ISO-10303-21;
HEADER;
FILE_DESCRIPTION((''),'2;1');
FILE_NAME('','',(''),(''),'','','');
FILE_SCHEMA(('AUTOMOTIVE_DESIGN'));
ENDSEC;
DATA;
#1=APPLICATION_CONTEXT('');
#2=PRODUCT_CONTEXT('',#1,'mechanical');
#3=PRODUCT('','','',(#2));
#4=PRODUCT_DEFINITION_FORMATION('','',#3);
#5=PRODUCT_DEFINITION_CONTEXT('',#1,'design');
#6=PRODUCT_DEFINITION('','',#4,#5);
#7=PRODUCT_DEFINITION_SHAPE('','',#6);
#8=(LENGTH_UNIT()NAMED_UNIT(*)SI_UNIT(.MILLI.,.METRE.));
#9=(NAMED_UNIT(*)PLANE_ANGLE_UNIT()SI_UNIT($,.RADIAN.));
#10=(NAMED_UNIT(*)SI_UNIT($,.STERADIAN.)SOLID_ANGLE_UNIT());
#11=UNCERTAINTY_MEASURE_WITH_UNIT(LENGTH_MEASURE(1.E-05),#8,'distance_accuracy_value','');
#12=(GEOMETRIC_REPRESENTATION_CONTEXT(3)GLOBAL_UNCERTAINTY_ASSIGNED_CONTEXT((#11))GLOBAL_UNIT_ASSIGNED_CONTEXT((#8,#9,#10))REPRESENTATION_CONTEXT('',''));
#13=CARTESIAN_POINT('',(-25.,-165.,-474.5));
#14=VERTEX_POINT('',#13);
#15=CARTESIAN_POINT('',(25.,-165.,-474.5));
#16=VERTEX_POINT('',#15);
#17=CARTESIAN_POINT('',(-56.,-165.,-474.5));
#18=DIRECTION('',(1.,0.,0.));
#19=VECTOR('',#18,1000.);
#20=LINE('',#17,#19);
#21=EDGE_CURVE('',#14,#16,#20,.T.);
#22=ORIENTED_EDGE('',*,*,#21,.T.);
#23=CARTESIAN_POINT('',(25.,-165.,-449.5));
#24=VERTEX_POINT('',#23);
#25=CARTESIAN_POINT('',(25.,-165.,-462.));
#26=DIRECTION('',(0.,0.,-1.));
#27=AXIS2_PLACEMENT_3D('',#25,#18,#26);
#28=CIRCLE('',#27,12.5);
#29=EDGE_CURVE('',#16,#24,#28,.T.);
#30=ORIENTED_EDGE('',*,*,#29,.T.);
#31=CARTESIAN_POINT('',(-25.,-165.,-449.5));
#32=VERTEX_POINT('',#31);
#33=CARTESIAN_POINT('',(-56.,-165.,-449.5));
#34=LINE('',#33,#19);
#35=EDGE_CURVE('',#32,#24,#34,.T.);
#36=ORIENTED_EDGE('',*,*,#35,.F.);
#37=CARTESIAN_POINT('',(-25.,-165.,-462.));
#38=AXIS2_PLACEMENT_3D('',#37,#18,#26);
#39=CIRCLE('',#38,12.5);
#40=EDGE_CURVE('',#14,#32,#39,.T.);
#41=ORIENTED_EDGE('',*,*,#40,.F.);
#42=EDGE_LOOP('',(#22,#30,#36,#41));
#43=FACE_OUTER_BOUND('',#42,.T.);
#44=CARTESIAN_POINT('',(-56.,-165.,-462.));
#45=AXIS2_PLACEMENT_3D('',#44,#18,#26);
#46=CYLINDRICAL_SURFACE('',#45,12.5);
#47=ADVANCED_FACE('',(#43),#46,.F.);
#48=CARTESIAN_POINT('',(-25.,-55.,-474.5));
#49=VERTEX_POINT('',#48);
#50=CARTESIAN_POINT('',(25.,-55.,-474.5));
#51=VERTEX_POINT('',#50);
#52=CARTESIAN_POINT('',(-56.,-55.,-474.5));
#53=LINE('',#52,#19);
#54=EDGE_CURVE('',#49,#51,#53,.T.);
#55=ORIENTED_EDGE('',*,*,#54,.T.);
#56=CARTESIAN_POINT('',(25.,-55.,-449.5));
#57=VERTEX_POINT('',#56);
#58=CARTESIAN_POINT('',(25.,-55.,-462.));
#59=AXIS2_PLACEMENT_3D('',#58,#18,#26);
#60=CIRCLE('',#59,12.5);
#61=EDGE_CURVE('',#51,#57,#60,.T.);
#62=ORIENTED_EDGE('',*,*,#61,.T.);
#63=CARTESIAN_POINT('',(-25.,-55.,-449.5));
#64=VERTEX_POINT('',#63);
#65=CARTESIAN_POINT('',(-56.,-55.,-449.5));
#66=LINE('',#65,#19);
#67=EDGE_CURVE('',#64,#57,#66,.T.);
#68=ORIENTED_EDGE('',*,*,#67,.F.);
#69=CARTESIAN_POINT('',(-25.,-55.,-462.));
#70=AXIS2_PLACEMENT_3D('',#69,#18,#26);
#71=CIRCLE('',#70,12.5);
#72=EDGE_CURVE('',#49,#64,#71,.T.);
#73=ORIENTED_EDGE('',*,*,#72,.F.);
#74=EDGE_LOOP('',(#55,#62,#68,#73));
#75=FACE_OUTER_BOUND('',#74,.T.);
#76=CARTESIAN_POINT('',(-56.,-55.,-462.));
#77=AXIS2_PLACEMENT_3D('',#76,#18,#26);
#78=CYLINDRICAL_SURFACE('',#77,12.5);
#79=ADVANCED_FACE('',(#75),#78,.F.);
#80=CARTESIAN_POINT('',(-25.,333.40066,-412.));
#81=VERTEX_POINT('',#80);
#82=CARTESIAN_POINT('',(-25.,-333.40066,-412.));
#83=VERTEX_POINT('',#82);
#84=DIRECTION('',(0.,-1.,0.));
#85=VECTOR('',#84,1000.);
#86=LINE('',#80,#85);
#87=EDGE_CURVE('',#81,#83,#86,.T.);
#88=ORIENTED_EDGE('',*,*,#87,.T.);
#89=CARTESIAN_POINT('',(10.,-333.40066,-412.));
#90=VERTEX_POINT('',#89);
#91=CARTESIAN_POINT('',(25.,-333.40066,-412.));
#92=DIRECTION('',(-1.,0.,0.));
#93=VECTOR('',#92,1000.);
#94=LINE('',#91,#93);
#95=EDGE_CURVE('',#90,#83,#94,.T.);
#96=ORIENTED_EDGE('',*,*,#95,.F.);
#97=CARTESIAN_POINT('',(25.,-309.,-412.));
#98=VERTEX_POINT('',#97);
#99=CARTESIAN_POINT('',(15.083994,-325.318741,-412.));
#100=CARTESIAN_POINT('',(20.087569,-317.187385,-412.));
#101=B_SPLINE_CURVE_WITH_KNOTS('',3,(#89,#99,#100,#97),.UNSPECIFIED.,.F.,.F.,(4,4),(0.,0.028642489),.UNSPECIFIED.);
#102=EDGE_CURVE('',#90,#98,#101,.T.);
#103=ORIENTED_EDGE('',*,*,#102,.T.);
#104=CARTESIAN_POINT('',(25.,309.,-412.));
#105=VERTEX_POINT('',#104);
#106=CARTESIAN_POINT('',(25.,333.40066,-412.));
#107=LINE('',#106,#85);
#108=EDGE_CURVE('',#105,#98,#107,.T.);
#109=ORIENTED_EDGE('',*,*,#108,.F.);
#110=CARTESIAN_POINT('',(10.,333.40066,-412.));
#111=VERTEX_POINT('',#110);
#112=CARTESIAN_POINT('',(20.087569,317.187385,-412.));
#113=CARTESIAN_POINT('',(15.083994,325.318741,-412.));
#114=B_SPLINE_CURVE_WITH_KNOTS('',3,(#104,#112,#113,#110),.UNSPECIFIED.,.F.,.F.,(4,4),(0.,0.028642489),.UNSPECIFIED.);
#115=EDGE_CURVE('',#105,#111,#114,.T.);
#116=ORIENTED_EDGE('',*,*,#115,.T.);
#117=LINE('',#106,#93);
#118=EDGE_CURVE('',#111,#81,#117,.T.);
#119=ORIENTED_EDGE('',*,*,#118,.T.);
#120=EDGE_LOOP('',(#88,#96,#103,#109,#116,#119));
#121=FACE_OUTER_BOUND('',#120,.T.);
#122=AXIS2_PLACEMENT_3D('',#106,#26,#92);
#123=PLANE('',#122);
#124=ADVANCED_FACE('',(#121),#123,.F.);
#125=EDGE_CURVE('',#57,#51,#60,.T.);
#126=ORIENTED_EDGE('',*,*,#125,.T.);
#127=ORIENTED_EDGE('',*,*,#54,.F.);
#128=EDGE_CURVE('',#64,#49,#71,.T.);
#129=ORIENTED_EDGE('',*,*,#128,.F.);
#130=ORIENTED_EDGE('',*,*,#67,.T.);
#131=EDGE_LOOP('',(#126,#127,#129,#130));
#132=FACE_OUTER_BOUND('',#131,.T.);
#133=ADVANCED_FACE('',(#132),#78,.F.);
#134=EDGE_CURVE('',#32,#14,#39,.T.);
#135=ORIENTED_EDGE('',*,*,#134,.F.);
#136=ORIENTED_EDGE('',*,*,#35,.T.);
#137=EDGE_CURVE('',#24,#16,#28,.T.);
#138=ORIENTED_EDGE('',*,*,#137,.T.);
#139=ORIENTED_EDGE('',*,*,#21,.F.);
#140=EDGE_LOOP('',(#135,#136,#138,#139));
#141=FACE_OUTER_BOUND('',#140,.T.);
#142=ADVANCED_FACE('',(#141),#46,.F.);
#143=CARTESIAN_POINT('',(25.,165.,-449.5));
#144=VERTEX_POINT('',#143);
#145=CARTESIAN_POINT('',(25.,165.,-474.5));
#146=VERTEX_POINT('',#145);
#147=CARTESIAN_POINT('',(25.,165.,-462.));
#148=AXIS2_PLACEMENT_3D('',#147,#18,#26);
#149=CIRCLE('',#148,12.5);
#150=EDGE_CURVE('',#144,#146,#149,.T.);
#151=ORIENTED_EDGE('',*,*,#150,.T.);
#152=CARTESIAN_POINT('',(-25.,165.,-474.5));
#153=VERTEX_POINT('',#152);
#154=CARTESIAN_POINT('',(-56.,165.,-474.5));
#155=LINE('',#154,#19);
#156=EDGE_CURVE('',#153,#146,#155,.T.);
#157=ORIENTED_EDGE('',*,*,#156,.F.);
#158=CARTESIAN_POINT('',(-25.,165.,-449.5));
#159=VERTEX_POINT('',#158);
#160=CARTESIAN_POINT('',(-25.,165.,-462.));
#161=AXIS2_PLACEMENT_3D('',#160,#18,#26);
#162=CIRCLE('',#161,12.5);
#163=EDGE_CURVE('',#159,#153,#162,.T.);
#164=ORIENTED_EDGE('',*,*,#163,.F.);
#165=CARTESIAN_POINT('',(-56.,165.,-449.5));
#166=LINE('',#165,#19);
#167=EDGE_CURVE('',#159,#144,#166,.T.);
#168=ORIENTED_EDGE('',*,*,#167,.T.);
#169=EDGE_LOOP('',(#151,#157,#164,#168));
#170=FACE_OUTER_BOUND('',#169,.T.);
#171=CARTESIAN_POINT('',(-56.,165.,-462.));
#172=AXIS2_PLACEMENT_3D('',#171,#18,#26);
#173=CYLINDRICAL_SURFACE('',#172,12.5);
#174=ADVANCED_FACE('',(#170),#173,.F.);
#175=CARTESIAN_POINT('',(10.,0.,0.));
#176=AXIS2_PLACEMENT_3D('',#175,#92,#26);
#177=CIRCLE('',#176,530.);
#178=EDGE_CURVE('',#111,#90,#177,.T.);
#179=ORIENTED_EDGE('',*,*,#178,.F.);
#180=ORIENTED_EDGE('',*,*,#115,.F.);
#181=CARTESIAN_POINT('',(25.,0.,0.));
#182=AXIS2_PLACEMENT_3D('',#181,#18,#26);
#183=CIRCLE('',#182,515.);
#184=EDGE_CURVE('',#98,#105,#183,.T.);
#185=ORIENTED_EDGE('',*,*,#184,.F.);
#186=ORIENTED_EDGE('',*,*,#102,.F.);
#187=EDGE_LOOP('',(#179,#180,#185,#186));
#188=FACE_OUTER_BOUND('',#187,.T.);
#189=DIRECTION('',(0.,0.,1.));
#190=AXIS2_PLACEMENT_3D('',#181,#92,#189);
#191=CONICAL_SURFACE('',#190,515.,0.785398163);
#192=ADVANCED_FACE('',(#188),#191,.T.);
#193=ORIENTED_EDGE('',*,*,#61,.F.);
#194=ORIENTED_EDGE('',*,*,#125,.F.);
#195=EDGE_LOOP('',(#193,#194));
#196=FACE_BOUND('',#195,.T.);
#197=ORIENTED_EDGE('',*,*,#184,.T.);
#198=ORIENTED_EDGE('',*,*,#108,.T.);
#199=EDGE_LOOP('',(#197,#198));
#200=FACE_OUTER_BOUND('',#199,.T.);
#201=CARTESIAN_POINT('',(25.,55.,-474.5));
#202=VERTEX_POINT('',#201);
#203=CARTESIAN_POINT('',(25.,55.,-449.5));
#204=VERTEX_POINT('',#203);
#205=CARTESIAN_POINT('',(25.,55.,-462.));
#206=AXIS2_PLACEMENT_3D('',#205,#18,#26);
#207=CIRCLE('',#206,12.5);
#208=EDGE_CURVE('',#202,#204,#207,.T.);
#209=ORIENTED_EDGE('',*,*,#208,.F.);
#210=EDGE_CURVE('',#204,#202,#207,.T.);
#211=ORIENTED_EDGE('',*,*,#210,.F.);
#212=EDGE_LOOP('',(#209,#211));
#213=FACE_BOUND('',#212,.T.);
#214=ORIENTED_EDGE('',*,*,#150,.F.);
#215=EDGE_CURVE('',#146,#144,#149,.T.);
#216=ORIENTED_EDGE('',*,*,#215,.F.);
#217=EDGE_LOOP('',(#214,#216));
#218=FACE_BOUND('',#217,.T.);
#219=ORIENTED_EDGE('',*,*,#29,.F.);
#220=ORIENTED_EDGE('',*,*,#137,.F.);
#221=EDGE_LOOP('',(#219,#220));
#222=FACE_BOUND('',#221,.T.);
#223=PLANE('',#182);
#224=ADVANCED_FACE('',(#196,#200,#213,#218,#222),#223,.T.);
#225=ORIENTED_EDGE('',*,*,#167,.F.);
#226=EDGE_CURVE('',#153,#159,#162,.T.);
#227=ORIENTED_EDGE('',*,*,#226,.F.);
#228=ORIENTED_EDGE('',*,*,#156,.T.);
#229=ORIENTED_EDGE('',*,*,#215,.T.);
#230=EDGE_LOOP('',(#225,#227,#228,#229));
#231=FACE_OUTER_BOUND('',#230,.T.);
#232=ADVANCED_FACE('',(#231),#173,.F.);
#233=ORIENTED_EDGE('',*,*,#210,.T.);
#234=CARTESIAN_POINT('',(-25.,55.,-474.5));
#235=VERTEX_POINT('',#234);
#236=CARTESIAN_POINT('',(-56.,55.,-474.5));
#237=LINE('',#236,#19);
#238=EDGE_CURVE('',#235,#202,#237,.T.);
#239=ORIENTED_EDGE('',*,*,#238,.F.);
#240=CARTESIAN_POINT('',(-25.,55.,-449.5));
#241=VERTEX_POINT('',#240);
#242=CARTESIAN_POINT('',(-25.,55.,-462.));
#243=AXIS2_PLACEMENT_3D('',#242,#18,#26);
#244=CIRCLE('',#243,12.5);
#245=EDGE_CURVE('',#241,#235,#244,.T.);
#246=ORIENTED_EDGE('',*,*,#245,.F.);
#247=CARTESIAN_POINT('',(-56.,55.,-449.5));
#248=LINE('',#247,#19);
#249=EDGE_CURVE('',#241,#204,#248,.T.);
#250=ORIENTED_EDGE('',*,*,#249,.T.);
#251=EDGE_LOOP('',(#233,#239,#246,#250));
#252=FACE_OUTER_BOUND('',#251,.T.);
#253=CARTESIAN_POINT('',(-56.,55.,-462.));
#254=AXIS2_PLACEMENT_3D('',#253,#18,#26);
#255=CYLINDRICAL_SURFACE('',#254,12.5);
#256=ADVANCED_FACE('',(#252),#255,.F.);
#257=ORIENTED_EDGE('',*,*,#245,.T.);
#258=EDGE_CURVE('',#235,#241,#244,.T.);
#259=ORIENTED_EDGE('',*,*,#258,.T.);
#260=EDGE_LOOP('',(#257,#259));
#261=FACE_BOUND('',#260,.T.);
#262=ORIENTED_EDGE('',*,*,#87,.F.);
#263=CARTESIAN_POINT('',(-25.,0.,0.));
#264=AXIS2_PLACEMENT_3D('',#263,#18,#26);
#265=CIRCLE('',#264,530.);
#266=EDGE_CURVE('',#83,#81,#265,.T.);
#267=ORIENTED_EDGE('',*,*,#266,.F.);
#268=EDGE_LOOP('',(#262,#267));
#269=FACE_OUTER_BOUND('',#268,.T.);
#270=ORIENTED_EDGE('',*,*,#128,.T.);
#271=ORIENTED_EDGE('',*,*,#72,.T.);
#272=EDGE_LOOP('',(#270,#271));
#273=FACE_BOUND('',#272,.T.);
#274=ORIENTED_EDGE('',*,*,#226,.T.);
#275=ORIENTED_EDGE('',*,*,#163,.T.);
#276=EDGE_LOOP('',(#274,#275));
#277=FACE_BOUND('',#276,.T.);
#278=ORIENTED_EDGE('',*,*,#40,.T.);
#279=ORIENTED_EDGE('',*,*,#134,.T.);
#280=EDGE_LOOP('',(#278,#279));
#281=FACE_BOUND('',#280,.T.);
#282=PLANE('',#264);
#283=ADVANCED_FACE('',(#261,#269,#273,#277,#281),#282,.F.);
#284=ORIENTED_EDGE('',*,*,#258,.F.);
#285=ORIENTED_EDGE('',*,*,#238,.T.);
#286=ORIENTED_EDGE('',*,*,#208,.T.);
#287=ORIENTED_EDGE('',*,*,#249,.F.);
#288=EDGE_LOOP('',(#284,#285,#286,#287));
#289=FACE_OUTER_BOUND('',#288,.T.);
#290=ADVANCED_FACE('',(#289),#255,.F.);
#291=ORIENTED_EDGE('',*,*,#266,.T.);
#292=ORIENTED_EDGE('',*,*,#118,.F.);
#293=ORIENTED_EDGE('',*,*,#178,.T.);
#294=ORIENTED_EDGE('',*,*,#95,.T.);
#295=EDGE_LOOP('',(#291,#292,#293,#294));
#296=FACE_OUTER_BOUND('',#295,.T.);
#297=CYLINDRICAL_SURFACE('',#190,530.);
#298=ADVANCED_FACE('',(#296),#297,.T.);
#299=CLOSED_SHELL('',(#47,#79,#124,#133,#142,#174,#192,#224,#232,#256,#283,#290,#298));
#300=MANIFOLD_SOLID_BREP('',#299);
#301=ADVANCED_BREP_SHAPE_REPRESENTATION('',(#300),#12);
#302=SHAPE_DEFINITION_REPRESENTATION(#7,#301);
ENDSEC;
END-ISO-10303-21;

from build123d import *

# Parameters (mm, degrees)
BOSS_EXTRUDE1_DEPTH = 25
SKETCH2_R           = 12.5
CUT_EXTRUDE1_DEPTH  = 81
CHAMFER2_SIZE       = 15


with BuildPart() as part:
    # Sketch1 → Boss-Extrude1 (new, symmetric)
    with BuildSketch(Plane(origin=(0, 0, 0), x_dir=(0, 0, -1), z_dir=(1, 0, 0))):
        with BuildLine():
            Line((412, 333.400659867), (412, -333.400659867))
            ThreePointArc((412, -333.400659867), (530, 0), (412, 333.400659867))
        make_face()
    extrude(amount=BOSS_EXTRUDE1_DEPTH, both=True)

    # Sketch2 → Cut-Extrude1 (cut)
    with BuildSketch(Plane(origin=(25, 0, 0), x_dir=(0, 0, -1), z_dir=(1, 0, 0))):
        with Locations((462, 55)):
            Circle(SKETCH2_R)
        with Locations((462, -55)):
            Circle(SKETCH2_R)
        with Locations((462, 165)):
            Circle(SKETCH2_R)
        with Locations((462, -165)):
            Circle(SKETCH2_R)
    extrude(amount=-CUT_EXTRUDE1_DEPTH, mode=Mode.SUBTRACT)

    # Chamfer2
    chamfer2_edges = [part.edges().sort_by_distance(p)[0] for p in [
        (25, 0, -530),
    ]]
    chamfer(chamfer2_edges, length=CHAMFER2_SIZE)


solid = part.part
